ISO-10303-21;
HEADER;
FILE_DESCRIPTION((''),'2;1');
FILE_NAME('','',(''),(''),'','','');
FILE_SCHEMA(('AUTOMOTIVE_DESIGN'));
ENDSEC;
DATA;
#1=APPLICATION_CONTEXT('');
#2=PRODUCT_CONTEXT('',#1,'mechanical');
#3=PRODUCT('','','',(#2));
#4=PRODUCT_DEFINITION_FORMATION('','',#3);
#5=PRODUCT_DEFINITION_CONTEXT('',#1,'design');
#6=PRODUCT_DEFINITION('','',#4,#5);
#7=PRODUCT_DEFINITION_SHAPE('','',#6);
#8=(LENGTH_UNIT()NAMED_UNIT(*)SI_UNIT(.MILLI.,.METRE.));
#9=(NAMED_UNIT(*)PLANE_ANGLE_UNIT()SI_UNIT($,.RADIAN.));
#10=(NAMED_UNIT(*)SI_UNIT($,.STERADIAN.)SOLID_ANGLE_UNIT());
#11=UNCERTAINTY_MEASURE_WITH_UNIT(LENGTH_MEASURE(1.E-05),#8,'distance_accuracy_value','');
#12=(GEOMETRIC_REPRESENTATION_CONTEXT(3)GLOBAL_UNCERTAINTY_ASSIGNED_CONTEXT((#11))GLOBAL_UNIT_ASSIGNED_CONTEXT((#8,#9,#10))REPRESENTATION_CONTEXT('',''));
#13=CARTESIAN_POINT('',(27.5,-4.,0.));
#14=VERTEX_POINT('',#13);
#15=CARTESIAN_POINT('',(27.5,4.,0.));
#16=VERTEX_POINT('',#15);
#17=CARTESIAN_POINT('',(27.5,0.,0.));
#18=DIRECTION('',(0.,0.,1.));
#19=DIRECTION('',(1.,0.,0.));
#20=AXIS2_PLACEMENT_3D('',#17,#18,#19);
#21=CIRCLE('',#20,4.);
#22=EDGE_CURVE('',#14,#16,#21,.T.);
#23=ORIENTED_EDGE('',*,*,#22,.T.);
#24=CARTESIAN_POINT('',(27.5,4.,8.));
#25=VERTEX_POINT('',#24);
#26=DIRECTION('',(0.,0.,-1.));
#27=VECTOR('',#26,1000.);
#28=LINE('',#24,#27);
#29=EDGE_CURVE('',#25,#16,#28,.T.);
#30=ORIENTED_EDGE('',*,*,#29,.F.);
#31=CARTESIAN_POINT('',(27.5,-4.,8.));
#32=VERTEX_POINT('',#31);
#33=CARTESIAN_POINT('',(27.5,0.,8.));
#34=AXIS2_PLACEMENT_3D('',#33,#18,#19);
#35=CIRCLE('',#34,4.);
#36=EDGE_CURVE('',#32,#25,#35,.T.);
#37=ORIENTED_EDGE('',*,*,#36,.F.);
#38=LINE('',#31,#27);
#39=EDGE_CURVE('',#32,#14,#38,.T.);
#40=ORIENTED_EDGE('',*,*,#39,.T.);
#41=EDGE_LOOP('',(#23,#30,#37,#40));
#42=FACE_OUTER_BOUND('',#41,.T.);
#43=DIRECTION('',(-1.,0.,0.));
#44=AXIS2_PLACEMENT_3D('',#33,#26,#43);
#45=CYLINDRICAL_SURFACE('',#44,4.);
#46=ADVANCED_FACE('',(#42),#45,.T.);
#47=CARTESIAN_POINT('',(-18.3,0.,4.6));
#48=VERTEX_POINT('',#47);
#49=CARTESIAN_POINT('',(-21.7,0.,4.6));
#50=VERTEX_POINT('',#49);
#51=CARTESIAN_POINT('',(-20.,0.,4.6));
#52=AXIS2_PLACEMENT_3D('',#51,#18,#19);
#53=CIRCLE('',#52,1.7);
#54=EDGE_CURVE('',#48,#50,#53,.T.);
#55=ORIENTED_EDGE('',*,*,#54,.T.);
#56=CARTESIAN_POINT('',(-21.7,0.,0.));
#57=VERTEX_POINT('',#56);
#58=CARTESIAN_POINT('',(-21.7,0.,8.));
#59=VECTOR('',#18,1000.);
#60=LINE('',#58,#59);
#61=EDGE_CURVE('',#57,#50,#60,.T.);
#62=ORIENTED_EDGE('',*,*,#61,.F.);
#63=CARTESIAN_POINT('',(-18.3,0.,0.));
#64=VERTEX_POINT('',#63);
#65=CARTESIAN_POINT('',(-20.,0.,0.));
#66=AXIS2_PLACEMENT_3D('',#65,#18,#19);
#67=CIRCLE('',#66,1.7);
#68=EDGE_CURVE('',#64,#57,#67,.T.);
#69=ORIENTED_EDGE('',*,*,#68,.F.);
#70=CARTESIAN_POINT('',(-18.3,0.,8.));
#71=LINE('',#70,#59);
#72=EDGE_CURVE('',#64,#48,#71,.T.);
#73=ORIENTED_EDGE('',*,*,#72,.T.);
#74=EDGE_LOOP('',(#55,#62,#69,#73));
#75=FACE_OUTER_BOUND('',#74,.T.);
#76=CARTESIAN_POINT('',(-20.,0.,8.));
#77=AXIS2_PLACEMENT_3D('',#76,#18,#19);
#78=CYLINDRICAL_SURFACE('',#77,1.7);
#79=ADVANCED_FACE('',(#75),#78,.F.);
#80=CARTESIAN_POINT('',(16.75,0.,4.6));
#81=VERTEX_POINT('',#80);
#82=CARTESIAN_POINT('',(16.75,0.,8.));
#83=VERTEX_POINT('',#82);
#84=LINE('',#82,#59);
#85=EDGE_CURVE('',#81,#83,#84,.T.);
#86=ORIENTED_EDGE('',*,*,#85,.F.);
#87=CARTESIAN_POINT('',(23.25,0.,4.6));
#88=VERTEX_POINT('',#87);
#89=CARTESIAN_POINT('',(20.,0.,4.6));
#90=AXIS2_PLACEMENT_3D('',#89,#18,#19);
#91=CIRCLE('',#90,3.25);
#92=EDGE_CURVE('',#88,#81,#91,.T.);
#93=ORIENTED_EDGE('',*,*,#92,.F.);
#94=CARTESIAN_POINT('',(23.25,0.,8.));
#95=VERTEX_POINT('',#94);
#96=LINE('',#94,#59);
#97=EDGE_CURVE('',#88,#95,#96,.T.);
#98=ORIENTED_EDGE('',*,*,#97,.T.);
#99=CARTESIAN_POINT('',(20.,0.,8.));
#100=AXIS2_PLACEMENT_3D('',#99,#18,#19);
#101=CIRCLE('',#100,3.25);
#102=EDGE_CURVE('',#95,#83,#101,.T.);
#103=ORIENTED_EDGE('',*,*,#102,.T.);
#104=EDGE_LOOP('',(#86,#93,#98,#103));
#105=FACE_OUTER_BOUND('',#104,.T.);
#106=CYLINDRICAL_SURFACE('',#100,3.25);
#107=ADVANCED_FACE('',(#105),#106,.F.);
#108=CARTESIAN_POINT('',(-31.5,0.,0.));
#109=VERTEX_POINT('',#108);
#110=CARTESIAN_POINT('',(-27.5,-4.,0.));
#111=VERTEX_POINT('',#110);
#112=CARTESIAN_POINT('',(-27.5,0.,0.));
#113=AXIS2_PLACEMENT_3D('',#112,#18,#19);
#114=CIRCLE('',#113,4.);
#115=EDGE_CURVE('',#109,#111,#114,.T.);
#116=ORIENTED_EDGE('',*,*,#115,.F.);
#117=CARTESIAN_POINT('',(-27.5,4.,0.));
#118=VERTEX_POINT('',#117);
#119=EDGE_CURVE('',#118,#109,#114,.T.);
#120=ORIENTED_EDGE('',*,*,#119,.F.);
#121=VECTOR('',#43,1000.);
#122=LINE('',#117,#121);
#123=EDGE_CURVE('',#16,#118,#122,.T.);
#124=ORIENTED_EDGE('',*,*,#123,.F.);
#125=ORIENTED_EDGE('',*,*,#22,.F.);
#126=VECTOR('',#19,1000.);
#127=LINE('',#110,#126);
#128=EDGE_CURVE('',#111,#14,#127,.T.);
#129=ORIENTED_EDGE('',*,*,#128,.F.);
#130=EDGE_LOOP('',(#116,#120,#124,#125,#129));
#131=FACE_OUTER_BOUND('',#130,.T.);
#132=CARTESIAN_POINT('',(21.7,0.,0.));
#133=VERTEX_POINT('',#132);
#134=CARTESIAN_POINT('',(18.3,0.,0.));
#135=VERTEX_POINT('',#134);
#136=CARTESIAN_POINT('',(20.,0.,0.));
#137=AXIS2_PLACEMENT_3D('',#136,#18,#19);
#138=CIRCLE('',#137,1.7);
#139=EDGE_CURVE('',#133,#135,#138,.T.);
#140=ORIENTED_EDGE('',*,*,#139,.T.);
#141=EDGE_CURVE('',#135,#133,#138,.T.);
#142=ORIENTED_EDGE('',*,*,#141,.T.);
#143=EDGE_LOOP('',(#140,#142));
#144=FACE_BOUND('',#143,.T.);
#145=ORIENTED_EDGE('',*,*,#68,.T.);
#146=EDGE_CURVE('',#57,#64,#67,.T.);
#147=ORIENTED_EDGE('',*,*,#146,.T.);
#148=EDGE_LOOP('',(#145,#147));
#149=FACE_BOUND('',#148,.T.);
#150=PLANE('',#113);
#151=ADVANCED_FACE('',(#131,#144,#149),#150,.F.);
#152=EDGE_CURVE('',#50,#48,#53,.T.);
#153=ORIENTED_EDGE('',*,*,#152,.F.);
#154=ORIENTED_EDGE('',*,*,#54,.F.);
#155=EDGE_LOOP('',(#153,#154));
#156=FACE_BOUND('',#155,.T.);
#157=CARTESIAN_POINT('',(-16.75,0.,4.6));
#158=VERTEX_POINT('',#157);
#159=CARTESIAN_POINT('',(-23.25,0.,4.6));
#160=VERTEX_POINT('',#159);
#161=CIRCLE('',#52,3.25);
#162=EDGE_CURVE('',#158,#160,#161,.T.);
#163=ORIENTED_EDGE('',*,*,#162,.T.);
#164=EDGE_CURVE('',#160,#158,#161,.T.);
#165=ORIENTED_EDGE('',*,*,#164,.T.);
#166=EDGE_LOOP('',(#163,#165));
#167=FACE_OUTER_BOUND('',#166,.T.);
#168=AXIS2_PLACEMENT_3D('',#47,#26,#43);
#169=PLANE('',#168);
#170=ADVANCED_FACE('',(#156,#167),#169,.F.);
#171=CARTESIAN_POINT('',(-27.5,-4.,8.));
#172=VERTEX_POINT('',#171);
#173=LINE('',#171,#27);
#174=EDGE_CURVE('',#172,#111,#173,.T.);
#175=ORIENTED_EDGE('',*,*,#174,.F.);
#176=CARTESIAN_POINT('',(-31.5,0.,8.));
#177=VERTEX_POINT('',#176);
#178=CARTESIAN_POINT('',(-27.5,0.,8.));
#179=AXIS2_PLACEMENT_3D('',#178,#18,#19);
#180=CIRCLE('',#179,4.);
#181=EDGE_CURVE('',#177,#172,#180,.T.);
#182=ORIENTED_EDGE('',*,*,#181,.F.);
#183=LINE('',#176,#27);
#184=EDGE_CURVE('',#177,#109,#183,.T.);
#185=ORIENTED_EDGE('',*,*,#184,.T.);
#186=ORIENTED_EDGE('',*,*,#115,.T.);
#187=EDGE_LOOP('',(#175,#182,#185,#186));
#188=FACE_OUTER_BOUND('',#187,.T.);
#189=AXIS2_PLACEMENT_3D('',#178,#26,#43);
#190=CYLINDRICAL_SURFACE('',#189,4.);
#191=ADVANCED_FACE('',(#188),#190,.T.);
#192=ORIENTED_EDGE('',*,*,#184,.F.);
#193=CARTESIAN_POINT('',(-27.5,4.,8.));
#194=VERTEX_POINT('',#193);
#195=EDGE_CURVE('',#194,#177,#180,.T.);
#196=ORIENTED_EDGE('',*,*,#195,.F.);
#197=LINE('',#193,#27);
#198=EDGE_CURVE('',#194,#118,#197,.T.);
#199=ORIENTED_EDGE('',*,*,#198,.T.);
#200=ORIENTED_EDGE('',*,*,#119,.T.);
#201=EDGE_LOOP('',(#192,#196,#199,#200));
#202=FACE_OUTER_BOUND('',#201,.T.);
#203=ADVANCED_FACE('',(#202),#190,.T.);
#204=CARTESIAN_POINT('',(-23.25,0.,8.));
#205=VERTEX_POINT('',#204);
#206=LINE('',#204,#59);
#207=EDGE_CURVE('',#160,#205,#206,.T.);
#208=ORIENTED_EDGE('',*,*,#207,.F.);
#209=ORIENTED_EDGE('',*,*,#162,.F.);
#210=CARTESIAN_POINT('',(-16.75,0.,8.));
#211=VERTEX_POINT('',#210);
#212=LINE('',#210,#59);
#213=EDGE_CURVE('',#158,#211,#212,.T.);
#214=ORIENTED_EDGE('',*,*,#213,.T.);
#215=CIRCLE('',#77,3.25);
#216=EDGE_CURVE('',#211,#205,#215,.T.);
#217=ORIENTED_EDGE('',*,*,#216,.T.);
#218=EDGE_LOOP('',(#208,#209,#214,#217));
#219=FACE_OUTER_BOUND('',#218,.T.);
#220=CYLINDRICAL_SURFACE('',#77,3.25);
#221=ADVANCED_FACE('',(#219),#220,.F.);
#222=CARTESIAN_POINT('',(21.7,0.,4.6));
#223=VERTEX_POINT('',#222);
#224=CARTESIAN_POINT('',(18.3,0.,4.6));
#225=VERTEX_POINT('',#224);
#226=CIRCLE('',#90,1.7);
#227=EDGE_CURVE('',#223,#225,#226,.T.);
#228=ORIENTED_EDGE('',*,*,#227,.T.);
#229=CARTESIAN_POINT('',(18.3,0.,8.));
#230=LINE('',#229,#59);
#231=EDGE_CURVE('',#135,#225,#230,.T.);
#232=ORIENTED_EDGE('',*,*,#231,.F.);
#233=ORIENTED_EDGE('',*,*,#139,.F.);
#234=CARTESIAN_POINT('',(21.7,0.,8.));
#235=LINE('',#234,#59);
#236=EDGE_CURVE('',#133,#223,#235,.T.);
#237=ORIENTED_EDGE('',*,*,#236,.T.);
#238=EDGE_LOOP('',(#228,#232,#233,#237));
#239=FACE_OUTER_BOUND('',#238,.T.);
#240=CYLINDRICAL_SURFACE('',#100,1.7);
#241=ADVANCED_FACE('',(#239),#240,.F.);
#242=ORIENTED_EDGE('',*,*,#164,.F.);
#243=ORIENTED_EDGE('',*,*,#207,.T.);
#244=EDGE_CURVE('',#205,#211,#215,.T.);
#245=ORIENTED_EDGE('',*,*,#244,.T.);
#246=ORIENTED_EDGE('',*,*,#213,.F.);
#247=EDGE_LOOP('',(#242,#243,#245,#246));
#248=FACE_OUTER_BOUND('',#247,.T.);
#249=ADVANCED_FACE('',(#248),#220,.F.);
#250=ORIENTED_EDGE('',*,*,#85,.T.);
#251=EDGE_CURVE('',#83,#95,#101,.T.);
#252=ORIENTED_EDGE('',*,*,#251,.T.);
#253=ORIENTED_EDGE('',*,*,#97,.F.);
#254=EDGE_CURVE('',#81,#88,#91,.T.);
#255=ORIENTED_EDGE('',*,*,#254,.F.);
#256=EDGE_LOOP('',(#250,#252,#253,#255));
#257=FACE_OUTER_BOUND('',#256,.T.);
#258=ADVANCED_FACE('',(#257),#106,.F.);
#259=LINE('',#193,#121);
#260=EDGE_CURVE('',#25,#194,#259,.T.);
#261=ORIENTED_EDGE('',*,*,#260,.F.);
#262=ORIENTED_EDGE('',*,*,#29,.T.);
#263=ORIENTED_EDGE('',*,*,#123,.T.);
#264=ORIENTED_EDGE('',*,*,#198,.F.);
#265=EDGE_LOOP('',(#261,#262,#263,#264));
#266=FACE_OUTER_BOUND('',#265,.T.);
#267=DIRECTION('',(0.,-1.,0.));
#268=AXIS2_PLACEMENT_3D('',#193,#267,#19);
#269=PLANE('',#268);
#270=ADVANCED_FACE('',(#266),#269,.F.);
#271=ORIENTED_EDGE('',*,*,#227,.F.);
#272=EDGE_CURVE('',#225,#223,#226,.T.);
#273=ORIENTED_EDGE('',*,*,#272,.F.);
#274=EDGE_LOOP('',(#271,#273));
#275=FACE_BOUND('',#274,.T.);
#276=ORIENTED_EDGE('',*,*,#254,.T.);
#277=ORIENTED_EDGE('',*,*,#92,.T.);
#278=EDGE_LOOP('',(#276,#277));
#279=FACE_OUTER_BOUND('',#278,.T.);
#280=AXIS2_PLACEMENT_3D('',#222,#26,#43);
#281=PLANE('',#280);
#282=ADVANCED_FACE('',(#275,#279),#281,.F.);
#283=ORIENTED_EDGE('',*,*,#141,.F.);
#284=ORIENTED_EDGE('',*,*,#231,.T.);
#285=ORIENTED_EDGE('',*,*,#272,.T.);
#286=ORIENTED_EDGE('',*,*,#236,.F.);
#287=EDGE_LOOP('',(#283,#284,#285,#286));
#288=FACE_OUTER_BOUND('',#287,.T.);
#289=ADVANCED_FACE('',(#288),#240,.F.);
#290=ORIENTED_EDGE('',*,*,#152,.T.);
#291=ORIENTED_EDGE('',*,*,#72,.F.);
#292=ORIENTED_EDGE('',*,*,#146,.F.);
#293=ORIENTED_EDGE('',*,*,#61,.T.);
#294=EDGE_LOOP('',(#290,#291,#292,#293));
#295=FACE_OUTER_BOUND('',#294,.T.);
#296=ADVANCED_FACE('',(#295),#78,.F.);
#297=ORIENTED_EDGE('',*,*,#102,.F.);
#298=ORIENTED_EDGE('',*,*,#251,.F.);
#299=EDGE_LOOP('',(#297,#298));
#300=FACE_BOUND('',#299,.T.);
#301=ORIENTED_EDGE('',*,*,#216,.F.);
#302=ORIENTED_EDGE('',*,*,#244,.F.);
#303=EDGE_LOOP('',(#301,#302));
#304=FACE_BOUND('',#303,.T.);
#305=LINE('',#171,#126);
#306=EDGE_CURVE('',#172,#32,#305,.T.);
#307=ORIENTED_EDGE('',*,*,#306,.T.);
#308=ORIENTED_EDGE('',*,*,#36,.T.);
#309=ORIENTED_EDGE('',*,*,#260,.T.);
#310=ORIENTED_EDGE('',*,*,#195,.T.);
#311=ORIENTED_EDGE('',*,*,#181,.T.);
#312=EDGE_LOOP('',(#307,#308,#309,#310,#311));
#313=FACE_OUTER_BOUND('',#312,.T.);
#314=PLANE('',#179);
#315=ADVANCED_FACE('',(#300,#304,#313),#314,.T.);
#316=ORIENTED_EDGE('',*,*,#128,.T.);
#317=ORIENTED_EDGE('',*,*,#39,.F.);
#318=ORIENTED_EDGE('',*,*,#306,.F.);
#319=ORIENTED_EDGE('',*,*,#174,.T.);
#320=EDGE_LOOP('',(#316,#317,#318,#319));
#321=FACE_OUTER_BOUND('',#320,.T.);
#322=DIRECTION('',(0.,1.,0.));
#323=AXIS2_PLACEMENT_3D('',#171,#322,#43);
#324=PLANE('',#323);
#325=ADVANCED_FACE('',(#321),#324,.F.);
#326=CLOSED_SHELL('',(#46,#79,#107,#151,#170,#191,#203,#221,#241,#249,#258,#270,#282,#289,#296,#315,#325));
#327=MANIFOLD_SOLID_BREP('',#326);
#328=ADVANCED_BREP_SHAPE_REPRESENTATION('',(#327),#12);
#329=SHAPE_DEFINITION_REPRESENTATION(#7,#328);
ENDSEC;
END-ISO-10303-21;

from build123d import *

# Parameters (mm, degrees)
BOSS_EXTRUDE1_DEPTH                                 = 8
CBORE_FOR_M3_HEX_SOCKET_HEAD_CAP_SCREW1_D           = 3.4
CBORE_FOR_M3_HEX_SOCKET_HEAD_CAP_SCREW1_CBORE_D     = 6.5
CBORE_FOR_M3_HEX_SOCKET_HEAD_CAP_SCREW1_CBORE_DEPTH = 3.4


with BuildPart() as part:
    # Sketch1 → Boss-Extrude1 (new body)
    with BuildSketch(Plane.XY):
        with BuildLine():
            Line((-27.5, 4), (27.5, 4))
            ThreePointArc((27.5, 4), (31.5, 0), (27.5, -4))
            Line((27.5, -4), (-27.5, -4))
            ThreePointArc((-27.5, -4), (-31.5, 0), (-27.5, 4))
        make_face()
    extrude(amount=BOSS_EXTRUDE1_DEPTH)

    # CBORE for M3 Hex Socket Head Cap Screw1 (through all)
    with Locations(Plane.XY.offset(8)):
        with Locations((-20, 0), (20, 0)):
            CounterBoreHole(CBORE_FOR_M3_HEX_SOCKET_HEAD_CAP_SCREW1_D / 2, CBORE_FOR_M3_HEX_SOCKET_HEAD_CAP_SCREW1_CBORE_D / 2, CBORE_FOR_M3_HEX_SOCKET_HEAD_CAP_SCREW1_CBORE_DEPTH)


solid = part.part
